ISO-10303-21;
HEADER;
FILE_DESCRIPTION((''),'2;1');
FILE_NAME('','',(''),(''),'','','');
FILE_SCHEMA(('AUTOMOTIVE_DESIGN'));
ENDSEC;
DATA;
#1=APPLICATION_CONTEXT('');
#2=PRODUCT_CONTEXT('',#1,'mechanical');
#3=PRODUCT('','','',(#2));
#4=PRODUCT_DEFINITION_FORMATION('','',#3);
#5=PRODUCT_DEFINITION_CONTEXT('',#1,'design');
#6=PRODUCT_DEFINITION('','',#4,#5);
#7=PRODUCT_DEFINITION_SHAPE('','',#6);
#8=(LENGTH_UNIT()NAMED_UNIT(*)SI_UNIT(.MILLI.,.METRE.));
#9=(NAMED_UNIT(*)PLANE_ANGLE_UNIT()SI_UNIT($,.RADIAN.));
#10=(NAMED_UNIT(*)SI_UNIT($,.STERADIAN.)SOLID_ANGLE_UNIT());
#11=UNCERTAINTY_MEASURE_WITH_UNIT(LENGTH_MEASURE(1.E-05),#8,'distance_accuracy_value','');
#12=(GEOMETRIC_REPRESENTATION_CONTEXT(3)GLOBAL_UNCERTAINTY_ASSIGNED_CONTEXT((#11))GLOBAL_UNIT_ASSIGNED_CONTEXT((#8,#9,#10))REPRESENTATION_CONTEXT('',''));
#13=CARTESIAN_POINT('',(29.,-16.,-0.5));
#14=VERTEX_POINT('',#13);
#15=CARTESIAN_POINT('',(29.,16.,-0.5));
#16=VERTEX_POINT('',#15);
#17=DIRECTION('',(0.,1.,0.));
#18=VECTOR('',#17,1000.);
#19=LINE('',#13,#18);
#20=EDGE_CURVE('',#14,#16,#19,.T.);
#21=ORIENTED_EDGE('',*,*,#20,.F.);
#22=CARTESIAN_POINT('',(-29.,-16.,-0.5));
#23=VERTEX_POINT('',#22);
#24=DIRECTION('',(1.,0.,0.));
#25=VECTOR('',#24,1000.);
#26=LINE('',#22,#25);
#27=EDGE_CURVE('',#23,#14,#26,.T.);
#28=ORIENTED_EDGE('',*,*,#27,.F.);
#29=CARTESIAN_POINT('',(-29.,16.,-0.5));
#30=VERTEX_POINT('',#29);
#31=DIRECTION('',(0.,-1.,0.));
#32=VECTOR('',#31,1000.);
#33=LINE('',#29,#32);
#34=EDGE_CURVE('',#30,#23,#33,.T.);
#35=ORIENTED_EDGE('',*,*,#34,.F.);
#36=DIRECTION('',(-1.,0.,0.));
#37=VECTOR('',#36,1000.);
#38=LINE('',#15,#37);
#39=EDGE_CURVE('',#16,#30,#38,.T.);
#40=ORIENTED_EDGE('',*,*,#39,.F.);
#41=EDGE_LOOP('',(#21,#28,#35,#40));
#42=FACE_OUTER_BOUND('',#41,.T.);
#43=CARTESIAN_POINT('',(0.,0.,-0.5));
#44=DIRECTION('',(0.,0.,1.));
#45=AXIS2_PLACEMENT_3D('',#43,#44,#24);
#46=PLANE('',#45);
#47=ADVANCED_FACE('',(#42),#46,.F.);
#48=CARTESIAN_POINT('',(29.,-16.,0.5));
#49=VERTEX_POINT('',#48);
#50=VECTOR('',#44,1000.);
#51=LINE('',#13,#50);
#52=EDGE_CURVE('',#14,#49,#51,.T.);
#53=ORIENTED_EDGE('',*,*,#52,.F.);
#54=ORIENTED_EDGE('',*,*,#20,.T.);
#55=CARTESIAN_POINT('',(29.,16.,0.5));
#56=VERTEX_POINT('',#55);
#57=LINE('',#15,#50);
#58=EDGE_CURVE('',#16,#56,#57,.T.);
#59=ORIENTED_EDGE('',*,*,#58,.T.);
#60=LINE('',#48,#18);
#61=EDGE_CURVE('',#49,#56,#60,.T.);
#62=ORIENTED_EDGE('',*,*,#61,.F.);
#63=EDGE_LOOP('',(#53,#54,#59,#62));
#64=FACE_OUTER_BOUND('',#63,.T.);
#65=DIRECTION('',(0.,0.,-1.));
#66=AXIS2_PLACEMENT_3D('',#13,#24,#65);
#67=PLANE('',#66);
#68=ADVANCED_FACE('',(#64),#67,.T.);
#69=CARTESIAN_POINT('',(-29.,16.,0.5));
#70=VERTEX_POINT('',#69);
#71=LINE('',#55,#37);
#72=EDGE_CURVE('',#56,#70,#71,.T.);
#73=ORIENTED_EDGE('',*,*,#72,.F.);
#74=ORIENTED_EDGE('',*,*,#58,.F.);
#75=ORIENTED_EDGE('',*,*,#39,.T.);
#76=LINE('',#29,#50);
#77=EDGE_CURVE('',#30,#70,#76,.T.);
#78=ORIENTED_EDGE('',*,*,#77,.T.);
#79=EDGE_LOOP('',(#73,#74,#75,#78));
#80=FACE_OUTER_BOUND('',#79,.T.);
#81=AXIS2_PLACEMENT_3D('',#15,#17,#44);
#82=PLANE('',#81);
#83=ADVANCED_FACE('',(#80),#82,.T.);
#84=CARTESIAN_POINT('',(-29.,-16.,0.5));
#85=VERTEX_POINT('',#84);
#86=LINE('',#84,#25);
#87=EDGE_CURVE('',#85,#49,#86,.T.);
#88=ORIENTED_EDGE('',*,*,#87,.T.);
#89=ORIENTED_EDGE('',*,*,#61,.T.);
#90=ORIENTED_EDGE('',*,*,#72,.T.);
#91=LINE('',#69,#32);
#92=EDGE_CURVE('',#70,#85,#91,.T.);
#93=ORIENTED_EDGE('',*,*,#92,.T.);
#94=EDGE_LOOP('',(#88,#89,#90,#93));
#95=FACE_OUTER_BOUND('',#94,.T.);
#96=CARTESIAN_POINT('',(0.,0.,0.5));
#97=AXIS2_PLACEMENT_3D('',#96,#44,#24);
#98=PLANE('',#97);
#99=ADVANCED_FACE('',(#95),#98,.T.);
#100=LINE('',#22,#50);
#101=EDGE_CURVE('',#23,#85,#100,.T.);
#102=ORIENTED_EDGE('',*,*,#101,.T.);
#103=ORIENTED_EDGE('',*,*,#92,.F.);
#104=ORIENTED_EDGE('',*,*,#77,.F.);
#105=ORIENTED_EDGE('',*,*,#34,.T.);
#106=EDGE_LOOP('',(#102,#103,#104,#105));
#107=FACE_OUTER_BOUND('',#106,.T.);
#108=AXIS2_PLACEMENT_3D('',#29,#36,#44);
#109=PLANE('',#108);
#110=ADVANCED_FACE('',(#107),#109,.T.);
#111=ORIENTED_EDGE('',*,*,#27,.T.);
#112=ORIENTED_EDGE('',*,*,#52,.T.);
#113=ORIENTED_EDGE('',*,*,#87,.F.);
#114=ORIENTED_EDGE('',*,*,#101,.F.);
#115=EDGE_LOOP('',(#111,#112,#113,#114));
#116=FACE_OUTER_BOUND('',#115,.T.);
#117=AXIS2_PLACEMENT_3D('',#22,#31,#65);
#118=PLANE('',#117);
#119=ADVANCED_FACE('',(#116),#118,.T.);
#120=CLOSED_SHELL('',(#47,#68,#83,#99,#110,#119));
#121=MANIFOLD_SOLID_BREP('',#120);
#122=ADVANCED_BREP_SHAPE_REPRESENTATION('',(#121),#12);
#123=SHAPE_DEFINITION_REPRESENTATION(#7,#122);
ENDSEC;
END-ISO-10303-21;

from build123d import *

# Parameters (mm, degrees)
SKETCH_1_W      = 58
SKETCH_1_H      = 32
EXTRUDE_1_DEPTH = 0.5


with BuildPart() as part:
    # 草图1 → 凸台-拉伸1 (new, symmetric)
    with BuildSketch(Plane.XY):
        Rectangle(SKETCH_1_W, SKETCH_1_H)
    extrude(amount=EXTRUDE_1_DEPTH, both=True)


solid = part.part
